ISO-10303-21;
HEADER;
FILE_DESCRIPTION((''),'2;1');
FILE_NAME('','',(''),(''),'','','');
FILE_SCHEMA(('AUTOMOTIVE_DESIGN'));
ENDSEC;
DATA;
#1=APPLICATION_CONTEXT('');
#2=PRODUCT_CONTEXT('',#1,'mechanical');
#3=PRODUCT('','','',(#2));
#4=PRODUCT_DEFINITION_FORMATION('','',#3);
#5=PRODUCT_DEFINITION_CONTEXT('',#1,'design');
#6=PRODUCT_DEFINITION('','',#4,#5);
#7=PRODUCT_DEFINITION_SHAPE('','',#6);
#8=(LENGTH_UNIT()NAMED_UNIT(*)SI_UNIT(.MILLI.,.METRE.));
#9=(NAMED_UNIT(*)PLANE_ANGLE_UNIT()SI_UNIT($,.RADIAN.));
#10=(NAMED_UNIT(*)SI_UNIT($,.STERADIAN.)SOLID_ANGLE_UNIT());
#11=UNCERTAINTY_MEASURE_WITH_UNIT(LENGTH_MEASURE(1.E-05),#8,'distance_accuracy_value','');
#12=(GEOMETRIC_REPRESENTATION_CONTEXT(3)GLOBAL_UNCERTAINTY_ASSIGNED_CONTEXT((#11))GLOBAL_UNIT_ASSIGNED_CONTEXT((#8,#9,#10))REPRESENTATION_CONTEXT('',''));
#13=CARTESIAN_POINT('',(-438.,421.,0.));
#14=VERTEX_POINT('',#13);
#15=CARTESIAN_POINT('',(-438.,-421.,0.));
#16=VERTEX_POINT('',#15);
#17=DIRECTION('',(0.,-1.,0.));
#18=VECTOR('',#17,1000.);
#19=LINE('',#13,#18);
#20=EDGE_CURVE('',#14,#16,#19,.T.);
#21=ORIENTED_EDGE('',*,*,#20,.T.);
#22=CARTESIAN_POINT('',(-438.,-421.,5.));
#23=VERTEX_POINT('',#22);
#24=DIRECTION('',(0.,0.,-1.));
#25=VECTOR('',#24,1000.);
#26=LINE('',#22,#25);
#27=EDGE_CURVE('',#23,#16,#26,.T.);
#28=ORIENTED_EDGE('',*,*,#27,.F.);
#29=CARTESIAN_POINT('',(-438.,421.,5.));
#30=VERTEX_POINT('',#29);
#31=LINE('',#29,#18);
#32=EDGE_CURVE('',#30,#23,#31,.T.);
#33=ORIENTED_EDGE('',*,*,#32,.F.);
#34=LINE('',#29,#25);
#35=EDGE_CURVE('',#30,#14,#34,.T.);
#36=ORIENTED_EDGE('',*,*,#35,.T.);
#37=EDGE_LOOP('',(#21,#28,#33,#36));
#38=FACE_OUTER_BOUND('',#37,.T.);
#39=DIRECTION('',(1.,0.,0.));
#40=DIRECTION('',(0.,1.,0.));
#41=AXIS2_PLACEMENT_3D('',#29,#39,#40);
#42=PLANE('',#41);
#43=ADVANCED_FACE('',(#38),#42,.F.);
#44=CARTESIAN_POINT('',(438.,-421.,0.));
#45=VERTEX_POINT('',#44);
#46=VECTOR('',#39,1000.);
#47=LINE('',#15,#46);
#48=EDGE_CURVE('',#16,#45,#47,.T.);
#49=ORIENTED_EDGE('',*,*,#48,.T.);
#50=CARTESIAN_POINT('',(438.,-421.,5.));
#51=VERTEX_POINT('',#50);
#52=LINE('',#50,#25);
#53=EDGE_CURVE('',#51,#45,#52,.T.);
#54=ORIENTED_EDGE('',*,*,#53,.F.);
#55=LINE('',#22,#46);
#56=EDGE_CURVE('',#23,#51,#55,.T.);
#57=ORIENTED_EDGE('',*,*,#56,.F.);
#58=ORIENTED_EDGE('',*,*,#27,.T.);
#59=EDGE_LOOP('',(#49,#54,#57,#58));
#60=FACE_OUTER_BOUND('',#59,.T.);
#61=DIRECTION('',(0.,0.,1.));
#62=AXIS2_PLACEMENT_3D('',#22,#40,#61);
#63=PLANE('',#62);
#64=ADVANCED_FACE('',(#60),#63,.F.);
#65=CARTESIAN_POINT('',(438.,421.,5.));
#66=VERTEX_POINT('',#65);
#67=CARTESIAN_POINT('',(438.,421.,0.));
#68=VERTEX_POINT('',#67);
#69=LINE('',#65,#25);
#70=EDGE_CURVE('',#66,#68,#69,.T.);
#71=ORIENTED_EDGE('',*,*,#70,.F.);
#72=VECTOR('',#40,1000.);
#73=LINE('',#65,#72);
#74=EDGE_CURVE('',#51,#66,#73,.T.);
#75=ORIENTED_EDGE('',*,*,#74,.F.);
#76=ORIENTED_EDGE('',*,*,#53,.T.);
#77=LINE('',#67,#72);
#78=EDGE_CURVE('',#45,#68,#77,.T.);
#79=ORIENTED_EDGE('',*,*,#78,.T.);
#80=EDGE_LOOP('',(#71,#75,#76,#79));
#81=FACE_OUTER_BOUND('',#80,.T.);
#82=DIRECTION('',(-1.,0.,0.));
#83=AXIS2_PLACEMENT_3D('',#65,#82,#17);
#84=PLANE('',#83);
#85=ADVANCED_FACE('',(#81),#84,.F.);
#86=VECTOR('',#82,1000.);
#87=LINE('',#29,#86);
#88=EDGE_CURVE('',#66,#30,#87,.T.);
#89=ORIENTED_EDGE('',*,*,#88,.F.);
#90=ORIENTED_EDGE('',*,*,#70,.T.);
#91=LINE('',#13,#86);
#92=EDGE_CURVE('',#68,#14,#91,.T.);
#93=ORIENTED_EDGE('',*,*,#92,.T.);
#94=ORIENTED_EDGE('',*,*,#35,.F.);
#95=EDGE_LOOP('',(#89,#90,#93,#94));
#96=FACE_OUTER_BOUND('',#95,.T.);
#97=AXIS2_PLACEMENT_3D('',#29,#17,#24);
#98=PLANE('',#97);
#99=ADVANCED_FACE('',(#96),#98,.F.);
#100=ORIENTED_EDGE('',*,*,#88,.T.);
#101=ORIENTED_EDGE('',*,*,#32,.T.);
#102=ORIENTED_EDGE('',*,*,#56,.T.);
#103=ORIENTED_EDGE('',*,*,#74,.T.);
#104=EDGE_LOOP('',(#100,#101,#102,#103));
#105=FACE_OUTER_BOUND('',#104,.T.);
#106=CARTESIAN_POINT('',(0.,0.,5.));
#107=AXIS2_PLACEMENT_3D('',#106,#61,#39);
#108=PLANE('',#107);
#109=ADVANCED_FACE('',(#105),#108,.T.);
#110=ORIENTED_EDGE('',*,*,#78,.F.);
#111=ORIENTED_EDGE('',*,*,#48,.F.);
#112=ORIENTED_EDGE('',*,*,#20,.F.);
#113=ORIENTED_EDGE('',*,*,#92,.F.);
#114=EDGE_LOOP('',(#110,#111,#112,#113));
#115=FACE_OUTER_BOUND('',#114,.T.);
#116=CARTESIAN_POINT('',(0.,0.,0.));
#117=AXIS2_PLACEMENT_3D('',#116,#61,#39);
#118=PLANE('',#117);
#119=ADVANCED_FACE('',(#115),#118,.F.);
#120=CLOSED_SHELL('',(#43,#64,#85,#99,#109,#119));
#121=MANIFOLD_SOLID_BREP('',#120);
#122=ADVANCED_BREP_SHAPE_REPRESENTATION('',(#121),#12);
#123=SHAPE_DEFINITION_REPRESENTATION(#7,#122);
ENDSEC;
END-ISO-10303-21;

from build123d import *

# Parameters (mm, degrees)
SKETCH_1_W      = 876
SKETCH_1_H      = 842
EXTRUDE_1_DEPTH = 5


with BuildPart() as part:
    # 草图1 → 凸台-拉伸1 (new body)
    with BuildSketch(Plane.XY):
        Rectangle(SKETCH_1_W, SKETCH_1_H)
    extrude(amount=EXTRUDE_1_DEPTH)


solid = part.part
